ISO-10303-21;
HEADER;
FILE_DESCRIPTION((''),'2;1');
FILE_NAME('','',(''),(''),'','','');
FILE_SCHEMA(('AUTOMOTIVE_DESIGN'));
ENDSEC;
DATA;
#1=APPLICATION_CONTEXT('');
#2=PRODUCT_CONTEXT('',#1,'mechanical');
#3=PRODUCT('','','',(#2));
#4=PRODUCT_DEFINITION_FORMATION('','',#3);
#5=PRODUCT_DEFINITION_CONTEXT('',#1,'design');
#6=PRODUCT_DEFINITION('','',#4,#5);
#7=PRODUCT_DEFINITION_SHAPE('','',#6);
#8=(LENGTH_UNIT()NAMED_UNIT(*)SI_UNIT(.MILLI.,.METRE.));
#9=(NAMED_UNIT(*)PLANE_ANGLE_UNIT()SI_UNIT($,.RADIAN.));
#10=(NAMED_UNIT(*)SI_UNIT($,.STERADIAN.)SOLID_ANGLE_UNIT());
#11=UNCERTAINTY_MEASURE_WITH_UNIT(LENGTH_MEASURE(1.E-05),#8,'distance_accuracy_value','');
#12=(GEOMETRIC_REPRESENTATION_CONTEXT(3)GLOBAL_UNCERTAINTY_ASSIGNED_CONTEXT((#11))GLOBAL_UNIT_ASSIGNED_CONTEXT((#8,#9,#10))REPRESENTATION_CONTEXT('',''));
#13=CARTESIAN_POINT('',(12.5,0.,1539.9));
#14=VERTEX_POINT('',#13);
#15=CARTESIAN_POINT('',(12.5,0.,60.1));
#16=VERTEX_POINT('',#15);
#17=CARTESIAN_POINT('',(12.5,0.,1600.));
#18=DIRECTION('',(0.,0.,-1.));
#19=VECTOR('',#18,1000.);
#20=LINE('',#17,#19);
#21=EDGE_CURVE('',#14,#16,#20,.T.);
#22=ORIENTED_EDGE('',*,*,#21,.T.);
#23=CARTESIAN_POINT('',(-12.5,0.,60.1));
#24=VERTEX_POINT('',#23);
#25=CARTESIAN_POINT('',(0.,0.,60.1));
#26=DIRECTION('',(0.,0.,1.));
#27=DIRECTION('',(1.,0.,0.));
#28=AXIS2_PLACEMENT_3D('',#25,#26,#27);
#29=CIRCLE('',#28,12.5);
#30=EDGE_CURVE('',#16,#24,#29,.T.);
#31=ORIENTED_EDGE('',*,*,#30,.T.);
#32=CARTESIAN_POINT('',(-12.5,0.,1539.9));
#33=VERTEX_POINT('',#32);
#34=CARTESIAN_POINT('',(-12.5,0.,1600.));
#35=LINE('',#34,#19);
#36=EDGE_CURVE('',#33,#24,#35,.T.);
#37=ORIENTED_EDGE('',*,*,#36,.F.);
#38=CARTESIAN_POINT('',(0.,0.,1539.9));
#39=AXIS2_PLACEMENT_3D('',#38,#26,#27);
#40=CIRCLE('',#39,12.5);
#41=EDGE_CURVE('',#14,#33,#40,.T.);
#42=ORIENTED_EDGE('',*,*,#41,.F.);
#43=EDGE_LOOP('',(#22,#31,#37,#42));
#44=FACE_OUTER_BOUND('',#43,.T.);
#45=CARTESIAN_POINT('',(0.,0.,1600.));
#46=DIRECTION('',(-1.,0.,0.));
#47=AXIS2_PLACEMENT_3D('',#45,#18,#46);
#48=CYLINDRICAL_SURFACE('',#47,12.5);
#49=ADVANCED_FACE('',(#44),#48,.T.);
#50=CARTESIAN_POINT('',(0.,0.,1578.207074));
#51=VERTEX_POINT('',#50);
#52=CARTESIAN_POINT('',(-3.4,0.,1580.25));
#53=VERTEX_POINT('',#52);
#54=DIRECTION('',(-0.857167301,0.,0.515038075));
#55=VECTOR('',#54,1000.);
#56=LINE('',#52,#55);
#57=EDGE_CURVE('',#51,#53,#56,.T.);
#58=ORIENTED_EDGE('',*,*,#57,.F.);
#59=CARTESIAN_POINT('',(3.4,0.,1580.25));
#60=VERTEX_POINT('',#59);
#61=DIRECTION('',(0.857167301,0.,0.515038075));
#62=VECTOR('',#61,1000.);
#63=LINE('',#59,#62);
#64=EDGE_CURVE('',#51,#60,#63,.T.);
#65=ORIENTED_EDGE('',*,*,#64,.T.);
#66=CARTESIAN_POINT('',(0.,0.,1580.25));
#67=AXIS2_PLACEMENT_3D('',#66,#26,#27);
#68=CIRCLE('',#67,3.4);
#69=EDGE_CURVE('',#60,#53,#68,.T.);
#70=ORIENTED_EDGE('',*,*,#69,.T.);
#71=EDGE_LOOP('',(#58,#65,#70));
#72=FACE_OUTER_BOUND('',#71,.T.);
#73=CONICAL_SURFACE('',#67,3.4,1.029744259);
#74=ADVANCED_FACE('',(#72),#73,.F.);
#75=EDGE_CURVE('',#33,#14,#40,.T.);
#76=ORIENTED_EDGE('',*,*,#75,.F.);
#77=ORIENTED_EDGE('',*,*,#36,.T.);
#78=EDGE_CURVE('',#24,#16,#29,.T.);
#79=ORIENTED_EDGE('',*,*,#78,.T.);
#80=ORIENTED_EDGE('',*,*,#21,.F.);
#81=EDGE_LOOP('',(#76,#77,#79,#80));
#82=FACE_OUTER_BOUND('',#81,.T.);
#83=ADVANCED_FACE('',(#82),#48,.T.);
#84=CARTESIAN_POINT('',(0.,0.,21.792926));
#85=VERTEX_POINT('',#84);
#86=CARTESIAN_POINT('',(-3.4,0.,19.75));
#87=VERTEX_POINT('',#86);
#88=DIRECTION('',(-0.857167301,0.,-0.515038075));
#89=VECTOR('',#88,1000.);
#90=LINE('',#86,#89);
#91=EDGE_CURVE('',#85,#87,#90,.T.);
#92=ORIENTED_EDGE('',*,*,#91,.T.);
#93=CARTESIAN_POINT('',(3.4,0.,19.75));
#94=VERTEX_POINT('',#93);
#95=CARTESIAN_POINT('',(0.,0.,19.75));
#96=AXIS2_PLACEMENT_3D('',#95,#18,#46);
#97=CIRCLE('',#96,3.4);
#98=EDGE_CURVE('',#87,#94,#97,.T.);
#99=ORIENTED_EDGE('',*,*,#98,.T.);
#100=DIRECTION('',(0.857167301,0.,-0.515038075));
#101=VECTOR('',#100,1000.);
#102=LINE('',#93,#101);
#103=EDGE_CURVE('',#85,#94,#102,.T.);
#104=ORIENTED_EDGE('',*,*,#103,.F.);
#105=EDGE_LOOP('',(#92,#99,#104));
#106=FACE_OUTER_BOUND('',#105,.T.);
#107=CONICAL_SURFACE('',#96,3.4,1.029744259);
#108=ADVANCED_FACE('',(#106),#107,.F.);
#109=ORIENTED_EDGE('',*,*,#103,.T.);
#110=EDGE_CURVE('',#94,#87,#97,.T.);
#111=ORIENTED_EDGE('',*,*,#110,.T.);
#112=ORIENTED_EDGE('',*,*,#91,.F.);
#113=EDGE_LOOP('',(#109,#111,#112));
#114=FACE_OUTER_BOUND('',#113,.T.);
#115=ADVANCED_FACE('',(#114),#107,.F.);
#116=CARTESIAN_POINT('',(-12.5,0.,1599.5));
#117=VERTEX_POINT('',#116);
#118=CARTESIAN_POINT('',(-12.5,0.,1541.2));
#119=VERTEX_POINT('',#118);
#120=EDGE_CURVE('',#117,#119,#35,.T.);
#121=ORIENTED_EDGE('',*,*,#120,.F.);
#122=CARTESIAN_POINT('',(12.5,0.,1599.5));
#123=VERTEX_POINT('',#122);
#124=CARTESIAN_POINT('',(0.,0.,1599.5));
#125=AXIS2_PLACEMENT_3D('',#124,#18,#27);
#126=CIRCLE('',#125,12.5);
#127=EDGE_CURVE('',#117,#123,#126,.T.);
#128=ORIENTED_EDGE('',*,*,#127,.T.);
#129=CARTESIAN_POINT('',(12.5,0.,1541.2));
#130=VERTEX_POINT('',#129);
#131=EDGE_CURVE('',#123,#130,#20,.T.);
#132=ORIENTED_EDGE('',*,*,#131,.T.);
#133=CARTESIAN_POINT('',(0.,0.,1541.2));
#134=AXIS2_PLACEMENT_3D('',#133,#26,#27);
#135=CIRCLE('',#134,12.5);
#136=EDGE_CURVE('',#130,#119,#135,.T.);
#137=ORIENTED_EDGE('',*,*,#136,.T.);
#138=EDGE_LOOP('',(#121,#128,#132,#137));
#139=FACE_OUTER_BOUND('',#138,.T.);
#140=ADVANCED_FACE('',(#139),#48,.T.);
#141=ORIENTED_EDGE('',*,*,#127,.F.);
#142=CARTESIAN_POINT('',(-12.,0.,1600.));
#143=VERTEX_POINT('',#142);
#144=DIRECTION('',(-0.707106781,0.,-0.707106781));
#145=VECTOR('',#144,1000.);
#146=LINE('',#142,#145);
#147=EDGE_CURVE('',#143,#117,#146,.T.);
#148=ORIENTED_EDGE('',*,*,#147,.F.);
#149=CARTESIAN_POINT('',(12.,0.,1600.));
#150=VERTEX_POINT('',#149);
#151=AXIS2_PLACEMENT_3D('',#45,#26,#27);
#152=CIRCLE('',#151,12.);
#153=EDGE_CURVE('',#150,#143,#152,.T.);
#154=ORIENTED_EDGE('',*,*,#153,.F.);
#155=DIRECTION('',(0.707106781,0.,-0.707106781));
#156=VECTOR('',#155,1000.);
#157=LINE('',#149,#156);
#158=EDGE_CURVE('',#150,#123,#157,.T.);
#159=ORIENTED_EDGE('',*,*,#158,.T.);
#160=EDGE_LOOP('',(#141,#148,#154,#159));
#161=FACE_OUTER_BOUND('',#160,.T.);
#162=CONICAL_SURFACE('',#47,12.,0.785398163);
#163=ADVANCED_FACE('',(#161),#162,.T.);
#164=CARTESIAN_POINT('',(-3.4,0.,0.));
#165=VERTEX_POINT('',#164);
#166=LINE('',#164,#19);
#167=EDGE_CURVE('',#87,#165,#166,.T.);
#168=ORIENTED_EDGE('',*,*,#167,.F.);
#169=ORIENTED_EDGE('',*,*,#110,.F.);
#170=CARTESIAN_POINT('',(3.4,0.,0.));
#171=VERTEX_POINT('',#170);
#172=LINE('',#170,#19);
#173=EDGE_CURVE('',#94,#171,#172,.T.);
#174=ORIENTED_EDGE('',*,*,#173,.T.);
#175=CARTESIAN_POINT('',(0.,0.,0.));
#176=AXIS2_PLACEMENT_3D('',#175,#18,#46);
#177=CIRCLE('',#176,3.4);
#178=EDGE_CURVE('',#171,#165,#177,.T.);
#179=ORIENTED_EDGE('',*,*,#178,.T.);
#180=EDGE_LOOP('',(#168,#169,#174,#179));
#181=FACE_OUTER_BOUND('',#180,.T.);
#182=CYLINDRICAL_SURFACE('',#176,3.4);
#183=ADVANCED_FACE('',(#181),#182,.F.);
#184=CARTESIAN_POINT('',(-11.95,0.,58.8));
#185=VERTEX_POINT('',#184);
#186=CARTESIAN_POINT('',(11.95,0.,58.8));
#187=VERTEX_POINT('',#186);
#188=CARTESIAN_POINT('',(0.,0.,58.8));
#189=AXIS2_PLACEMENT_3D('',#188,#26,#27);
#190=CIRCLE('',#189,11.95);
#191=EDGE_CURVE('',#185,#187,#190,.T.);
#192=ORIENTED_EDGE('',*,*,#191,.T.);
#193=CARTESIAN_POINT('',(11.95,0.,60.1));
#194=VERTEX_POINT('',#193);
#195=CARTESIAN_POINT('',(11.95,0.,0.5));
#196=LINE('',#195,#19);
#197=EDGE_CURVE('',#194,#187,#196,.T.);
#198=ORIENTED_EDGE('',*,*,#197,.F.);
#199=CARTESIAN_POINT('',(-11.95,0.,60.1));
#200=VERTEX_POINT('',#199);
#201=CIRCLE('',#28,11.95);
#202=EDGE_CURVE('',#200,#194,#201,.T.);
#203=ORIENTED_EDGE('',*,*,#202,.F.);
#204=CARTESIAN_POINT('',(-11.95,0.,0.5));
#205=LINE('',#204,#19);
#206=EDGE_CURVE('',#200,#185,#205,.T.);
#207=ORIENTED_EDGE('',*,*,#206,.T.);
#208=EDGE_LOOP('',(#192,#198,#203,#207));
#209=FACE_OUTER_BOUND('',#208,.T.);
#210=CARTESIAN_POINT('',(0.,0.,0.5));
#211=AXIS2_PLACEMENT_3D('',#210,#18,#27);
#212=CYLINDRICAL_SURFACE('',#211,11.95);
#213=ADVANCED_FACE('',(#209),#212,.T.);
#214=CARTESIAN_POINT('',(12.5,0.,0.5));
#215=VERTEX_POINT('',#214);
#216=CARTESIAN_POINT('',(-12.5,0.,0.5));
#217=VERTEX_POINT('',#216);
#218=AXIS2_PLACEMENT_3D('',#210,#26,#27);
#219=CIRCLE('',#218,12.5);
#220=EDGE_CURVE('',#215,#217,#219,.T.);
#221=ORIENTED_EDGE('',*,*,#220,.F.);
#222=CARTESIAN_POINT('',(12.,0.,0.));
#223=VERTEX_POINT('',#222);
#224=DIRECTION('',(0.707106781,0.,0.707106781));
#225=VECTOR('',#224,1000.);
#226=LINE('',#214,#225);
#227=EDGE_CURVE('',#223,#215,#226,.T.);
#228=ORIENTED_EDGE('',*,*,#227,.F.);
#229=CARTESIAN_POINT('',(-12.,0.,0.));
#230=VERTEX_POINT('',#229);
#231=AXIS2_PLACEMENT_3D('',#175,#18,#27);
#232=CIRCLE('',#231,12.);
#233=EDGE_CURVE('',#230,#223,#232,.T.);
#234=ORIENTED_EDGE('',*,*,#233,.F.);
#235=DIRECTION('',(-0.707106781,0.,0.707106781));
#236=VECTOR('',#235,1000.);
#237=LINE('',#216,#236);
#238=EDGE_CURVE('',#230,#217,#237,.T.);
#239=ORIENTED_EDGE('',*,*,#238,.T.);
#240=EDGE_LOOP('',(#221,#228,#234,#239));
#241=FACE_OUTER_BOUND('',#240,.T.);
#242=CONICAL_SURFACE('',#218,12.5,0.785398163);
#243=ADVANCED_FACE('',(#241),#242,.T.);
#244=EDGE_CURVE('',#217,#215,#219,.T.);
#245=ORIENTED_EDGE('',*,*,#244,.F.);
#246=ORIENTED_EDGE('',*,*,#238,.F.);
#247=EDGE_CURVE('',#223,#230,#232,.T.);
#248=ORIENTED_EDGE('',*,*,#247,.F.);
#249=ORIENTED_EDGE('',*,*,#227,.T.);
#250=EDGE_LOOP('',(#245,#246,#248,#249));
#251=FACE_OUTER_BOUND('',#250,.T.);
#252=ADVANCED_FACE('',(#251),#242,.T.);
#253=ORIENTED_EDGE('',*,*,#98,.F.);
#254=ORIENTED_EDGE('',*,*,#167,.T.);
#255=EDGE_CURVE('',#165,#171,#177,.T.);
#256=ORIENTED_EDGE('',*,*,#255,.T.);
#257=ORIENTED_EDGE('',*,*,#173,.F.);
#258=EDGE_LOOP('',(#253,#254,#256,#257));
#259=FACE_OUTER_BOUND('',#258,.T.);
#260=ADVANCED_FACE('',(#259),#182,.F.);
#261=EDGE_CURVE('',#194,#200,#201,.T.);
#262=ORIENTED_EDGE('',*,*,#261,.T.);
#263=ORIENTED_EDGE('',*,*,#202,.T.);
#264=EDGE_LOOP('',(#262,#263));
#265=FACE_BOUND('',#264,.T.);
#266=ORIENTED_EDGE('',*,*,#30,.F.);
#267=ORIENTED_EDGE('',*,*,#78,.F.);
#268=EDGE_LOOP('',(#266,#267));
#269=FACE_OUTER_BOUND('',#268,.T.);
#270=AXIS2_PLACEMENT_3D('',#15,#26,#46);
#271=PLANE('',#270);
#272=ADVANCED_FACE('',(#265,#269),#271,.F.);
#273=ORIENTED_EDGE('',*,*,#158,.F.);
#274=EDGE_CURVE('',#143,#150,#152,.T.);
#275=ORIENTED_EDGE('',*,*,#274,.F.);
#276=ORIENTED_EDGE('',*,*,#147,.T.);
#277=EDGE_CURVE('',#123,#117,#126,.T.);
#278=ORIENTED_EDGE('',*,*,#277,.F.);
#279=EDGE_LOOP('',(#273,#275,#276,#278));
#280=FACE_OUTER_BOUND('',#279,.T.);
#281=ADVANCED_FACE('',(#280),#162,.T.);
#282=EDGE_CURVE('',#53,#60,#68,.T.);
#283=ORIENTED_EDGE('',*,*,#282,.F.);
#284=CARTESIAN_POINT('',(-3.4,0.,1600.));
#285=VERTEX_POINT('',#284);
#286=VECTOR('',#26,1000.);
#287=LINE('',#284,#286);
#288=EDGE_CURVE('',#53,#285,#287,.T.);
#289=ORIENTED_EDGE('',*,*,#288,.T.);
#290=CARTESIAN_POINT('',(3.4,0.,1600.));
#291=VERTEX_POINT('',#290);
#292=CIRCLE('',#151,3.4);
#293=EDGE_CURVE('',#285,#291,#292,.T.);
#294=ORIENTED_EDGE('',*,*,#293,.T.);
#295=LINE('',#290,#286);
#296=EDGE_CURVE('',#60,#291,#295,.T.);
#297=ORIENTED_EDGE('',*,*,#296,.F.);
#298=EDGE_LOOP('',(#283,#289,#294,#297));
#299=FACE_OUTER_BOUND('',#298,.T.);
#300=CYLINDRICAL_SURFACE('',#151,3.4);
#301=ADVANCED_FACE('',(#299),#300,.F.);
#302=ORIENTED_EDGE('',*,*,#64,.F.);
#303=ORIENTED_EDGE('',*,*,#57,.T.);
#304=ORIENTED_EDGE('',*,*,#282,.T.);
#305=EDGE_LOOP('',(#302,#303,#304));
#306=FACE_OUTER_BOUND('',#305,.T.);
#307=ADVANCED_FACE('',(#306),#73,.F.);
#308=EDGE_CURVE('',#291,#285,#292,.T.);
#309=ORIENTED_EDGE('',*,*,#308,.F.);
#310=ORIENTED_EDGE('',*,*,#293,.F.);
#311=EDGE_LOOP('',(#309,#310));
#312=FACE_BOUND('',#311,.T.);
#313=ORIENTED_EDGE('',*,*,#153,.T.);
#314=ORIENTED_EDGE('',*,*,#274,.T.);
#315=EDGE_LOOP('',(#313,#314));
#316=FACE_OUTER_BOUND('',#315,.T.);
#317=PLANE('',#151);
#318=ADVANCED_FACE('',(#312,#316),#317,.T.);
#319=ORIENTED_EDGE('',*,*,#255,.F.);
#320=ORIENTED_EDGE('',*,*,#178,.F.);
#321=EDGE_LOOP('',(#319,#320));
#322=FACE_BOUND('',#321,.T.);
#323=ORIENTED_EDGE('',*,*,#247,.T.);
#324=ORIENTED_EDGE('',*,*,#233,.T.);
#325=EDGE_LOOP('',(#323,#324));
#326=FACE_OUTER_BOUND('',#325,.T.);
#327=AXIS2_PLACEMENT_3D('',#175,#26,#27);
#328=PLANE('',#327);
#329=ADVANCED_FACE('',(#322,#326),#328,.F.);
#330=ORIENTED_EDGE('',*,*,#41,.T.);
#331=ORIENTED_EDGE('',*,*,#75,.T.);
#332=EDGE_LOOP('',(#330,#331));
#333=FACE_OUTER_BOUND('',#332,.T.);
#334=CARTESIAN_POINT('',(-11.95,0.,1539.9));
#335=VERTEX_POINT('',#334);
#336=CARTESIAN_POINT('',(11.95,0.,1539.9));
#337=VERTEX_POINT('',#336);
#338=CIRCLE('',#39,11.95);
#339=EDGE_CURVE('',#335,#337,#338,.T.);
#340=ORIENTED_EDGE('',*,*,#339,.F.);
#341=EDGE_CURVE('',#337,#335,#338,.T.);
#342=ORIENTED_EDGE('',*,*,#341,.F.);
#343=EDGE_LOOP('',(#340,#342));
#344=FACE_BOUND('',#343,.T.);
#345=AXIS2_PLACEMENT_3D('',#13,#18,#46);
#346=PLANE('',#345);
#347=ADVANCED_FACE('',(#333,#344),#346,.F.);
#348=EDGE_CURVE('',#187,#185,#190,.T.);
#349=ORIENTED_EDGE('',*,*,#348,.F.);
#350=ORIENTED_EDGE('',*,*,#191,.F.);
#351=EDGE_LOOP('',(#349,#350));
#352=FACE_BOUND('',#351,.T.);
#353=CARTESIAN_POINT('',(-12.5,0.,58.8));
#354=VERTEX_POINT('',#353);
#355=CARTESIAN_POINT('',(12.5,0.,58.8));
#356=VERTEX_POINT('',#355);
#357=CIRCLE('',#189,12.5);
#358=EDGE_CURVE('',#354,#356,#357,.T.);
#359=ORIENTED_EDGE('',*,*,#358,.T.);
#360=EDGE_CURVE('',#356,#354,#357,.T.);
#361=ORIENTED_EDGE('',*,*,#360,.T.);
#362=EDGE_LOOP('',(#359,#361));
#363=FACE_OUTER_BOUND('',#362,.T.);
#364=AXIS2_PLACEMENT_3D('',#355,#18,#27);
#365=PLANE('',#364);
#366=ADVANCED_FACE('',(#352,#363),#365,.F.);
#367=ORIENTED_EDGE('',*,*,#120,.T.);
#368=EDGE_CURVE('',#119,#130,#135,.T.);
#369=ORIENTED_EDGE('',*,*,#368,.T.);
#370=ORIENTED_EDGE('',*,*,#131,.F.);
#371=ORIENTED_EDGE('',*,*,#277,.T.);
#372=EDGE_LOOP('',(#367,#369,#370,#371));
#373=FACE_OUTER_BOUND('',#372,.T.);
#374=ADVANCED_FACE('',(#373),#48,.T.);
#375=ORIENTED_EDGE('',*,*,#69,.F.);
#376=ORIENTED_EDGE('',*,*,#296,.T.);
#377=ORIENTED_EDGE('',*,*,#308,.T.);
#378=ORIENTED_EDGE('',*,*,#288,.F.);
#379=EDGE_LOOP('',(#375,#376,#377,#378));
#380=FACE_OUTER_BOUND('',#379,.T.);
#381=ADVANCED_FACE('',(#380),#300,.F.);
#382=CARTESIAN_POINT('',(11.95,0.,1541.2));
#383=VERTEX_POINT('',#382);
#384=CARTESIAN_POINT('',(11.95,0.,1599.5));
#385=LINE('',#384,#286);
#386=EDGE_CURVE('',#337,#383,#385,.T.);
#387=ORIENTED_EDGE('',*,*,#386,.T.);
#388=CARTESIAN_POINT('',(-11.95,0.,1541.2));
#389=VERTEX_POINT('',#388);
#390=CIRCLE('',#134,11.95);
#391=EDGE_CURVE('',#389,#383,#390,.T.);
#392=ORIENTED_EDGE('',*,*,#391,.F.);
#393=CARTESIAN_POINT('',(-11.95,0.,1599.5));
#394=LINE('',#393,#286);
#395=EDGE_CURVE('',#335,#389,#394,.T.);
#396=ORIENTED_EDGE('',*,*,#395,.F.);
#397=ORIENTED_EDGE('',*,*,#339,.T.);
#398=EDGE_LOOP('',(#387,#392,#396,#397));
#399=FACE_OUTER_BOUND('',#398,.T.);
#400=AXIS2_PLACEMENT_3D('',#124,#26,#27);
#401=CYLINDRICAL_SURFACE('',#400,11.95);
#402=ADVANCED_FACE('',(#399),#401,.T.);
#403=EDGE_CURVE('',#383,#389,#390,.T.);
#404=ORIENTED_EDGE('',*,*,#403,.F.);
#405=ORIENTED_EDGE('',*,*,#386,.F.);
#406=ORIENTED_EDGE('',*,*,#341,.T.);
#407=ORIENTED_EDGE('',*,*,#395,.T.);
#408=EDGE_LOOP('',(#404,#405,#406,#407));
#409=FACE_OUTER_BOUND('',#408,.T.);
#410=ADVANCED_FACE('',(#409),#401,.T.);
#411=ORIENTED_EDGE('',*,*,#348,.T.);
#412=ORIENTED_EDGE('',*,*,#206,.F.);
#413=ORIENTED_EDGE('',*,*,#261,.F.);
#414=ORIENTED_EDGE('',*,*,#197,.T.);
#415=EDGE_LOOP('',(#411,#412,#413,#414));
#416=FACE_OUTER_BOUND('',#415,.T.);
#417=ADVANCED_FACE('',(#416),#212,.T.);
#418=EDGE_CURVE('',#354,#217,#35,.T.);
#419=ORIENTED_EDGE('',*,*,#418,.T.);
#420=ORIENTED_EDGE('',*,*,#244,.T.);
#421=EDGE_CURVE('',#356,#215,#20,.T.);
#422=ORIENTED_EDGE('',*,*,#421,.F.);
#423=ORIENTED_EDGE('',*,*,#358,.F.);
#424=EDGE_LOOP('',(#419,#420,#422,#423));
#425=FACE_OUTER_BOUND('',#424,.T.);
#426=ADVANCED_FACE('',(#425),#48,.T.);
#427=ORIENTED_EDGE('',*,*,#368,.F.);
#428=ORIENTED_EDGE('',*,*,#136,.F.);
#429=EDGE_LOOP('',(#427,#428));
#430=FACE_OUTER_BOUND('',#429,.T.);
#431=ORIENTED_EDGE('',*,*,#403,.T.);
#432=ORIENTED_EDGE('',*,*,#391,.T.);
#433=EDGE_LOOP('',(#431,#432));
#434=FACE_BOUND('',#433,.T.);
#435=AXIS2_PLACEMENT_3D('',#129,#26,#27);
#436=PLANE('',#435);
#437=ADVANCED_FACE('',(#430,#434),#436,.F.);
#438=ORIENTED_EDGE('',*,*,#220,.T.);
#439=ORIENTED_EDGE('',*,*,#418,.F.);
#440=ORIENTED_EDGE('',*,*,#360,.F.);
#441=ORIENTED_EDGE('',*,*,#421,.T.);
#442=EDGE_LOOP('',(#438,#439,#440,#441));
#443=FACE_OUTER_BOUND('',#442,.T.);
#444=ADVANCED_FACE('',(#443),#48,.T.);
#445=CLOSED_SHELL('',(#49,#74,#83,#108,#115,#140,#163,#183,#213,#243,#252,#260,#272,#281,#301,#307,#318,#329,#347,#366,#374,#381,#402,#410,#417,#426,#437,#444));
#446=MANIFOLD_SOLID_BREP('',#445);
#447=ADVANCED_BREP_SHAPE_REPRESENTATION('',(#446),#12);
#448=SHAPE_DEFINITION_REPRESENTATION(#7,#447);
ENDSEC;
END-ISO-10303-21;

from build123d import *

# Parameters (mm, degrees)
SKETCH_1_R      = 12.5
EXTRUDE_1_DEPTH = 1600
CHAMFER_1_SIZE  = 0.5
SKETCH_2_W      = 0.55
SKETCH_2_H      = 1.3


with BuildPart() as part:
    # 草图1 → 凸台-拉伸1 (new body)
    with BuildSketch(Plane.XY):
        Circle(SKETCH_1_R)
    extrude(amount=EXTRUDE_1_DEPTH)

    # 倒角1
    chamfer_1_edges = [part.edges().sort_by_distance(p)[0] for p in [
        (-12.5, 0, 0),
        (-12.5, 0, 1600),
    ]]
    chamfer(chamfer_1_edges, length=CHAMFER_1_SIZE)

    # 草图2 → 切除-旋转1 (revolve, cut)
    with BuildSketch(Plane(origin=(0, 0, 0), x_dir=(1, 0, 0), z_dir=(0, 1, 0))):
        with Locations((12.225, -1540.55)):
            Rectangle(SKETCH_2_W, SKETCH_2_H)
    cut_revolve_1 = revolve(axis=Axis((0, 0, 1599.5), (0, 0, -1)), mode=Mode.SUBTRACT)

    # 草图5 → M8 螺纹孔1 (revolve, cut)
    with BuildSketch(Plane(origin=(0, 0, 1600), x_dir=(0, -1, 0), z_dir=(1, 0, 0))):
        Polygon((0, 0), (0, 21.792926105), (3.4, 19.75), (3.4, 0), align=None)
    hole_wizard_m8_1 = revolve(axis=Axis((0, 0, 1606.35), (0, 0, -1)), mode=Mode.SUBTRACT)

    # 镜向1: 切除-旋转1, M8 螺纹孔1 across plane
    add(cut_revolve_1.mirror(Plane.XY.offset(800)), mode=Mode.SUBTRACT)
    add(hole_wizard_m8_1.mirror(Plane.XY.offset(800)), mode=Mode.SUBTRACT)


solid = part.part
